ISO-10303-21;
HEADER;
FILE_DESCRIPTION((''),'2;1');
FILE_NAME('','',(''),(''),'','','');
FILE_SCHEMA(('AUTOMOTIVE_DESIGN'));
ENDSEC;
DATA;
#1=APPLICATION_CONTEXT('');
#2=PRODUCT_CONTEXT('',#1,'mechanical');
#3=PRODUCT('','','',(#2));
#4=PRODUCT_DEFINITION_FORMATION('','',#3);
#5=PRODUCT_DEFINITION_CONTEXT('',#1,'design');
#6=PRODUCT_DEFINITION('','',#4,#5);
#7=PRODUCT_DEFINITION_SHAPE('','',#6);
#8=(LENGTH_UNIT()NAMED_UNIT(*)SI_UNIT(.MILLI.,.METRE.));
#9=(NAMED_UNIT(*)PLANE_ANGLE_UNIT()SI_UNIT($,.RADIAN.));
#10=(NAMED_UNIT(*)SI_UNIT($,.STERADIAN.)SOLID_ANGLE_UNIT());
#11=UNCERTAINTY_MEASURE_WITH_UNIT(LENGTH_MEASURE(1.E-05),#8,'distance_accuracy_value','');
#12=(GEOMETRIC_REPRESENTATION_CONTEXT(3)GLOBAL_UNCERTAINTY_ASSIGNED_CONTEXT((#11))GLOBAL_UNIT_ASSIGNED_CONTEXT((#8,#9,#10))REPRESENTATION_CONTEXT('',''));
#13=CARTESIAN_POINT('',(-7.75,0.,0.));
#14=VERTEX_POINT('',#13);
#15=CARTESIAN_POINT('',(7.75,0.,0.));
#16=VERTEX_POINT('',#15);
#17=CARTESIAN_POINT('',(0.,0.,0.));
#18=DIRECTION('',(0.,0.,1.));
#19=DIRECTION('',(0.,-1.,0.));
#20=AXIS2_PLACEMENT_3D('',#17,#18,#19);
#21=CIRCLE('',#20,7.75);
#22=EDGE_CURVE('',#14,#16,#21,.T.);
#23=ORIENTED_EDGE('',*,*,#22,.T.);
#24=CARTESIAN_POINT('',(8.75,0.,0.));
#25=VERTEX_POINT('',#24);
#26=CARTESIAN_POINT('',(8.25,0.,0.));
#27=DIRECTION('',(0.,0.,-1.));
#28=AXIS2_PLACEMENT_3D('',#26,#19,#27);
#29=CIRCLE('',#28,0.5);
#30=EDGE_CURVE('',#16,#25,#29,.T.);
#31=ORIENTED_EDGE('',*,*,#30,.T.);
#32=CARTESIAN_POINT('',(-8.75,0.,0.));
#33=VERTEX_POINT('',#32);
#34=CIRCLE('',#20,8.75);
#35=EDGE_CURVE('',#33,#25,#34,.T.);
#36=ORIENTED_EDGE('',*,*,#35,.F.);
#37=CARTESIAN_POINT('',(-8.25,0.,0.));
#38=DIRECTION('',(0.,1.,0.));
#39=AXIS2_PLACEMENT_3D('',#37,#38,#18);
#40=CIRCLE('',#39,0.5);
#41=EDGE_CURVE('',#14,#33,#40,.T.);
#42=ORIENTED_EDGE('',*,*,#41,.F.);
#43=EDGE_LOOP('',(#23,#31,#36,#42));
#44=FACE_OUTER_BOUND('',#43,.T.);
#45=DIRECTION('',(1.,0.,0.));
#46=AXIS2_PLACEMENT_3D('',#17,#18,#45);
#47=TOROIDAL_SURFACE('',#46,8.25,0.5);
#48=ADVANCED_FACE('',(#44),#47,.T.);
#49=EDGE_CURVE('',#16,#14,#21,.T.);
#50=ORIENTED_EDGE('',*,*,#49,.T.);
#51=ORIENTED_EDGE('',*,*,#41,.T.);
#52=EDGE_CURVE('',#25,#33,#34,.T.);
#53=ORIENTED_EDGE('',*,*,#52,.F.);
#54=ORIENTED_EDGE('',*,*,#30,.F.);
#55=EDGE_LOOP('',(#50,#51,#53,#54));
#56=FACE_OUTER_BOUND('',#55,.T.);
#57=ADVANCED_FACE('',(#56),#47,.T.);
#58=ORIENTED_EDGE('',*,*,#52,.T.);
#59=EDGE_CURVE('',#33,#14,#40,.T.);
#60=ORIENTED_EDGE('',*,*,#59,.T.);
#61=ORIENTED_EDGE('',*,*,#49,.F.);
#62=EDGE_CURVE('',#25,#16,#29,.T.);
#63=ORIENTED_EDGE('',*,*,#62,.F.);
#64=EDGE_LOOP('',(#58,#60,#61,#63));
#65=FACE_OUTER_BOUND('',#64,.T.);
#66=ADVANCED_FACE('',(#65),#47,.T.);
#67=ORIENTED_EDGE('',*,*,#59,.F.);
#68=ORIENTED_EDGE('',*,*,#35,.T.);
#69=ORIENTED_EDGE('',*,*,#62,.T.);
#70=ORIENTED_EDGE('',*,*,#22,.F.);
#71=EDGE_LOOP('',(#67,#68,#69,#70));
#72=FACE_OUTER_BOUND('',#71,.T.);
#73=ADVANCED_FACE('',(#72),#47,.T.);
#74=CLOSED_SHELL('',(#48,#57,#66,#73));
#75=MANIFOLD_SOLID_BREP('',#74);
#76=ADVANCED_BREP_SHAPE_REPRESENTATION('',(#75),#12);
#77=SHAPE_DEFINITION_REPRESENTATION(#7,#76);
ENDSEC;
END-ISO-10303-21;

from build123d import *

# Parameters (mm, degrees)
SKETCH2_R = 0.5


with BuildPart() as part:
    # Sweep1: sweep along a path in Sketch1
    with BuildLine(Plane.XY) as sweep1_path:
        CenterArc((0, 0), 8.25, 0, 360)
    # Sketch2 → Sweep1 (sweep)
    with BuildSketch(Plane(origin=(0, 0, 0), x_dir=(1, 0, 0), z_dir=(0, 1, 0))):
        with Locations((-8.25, 0)):
            Circle(SKETCH2_R)
    sweep(path=sweep1_path.line)


solid = part.part
